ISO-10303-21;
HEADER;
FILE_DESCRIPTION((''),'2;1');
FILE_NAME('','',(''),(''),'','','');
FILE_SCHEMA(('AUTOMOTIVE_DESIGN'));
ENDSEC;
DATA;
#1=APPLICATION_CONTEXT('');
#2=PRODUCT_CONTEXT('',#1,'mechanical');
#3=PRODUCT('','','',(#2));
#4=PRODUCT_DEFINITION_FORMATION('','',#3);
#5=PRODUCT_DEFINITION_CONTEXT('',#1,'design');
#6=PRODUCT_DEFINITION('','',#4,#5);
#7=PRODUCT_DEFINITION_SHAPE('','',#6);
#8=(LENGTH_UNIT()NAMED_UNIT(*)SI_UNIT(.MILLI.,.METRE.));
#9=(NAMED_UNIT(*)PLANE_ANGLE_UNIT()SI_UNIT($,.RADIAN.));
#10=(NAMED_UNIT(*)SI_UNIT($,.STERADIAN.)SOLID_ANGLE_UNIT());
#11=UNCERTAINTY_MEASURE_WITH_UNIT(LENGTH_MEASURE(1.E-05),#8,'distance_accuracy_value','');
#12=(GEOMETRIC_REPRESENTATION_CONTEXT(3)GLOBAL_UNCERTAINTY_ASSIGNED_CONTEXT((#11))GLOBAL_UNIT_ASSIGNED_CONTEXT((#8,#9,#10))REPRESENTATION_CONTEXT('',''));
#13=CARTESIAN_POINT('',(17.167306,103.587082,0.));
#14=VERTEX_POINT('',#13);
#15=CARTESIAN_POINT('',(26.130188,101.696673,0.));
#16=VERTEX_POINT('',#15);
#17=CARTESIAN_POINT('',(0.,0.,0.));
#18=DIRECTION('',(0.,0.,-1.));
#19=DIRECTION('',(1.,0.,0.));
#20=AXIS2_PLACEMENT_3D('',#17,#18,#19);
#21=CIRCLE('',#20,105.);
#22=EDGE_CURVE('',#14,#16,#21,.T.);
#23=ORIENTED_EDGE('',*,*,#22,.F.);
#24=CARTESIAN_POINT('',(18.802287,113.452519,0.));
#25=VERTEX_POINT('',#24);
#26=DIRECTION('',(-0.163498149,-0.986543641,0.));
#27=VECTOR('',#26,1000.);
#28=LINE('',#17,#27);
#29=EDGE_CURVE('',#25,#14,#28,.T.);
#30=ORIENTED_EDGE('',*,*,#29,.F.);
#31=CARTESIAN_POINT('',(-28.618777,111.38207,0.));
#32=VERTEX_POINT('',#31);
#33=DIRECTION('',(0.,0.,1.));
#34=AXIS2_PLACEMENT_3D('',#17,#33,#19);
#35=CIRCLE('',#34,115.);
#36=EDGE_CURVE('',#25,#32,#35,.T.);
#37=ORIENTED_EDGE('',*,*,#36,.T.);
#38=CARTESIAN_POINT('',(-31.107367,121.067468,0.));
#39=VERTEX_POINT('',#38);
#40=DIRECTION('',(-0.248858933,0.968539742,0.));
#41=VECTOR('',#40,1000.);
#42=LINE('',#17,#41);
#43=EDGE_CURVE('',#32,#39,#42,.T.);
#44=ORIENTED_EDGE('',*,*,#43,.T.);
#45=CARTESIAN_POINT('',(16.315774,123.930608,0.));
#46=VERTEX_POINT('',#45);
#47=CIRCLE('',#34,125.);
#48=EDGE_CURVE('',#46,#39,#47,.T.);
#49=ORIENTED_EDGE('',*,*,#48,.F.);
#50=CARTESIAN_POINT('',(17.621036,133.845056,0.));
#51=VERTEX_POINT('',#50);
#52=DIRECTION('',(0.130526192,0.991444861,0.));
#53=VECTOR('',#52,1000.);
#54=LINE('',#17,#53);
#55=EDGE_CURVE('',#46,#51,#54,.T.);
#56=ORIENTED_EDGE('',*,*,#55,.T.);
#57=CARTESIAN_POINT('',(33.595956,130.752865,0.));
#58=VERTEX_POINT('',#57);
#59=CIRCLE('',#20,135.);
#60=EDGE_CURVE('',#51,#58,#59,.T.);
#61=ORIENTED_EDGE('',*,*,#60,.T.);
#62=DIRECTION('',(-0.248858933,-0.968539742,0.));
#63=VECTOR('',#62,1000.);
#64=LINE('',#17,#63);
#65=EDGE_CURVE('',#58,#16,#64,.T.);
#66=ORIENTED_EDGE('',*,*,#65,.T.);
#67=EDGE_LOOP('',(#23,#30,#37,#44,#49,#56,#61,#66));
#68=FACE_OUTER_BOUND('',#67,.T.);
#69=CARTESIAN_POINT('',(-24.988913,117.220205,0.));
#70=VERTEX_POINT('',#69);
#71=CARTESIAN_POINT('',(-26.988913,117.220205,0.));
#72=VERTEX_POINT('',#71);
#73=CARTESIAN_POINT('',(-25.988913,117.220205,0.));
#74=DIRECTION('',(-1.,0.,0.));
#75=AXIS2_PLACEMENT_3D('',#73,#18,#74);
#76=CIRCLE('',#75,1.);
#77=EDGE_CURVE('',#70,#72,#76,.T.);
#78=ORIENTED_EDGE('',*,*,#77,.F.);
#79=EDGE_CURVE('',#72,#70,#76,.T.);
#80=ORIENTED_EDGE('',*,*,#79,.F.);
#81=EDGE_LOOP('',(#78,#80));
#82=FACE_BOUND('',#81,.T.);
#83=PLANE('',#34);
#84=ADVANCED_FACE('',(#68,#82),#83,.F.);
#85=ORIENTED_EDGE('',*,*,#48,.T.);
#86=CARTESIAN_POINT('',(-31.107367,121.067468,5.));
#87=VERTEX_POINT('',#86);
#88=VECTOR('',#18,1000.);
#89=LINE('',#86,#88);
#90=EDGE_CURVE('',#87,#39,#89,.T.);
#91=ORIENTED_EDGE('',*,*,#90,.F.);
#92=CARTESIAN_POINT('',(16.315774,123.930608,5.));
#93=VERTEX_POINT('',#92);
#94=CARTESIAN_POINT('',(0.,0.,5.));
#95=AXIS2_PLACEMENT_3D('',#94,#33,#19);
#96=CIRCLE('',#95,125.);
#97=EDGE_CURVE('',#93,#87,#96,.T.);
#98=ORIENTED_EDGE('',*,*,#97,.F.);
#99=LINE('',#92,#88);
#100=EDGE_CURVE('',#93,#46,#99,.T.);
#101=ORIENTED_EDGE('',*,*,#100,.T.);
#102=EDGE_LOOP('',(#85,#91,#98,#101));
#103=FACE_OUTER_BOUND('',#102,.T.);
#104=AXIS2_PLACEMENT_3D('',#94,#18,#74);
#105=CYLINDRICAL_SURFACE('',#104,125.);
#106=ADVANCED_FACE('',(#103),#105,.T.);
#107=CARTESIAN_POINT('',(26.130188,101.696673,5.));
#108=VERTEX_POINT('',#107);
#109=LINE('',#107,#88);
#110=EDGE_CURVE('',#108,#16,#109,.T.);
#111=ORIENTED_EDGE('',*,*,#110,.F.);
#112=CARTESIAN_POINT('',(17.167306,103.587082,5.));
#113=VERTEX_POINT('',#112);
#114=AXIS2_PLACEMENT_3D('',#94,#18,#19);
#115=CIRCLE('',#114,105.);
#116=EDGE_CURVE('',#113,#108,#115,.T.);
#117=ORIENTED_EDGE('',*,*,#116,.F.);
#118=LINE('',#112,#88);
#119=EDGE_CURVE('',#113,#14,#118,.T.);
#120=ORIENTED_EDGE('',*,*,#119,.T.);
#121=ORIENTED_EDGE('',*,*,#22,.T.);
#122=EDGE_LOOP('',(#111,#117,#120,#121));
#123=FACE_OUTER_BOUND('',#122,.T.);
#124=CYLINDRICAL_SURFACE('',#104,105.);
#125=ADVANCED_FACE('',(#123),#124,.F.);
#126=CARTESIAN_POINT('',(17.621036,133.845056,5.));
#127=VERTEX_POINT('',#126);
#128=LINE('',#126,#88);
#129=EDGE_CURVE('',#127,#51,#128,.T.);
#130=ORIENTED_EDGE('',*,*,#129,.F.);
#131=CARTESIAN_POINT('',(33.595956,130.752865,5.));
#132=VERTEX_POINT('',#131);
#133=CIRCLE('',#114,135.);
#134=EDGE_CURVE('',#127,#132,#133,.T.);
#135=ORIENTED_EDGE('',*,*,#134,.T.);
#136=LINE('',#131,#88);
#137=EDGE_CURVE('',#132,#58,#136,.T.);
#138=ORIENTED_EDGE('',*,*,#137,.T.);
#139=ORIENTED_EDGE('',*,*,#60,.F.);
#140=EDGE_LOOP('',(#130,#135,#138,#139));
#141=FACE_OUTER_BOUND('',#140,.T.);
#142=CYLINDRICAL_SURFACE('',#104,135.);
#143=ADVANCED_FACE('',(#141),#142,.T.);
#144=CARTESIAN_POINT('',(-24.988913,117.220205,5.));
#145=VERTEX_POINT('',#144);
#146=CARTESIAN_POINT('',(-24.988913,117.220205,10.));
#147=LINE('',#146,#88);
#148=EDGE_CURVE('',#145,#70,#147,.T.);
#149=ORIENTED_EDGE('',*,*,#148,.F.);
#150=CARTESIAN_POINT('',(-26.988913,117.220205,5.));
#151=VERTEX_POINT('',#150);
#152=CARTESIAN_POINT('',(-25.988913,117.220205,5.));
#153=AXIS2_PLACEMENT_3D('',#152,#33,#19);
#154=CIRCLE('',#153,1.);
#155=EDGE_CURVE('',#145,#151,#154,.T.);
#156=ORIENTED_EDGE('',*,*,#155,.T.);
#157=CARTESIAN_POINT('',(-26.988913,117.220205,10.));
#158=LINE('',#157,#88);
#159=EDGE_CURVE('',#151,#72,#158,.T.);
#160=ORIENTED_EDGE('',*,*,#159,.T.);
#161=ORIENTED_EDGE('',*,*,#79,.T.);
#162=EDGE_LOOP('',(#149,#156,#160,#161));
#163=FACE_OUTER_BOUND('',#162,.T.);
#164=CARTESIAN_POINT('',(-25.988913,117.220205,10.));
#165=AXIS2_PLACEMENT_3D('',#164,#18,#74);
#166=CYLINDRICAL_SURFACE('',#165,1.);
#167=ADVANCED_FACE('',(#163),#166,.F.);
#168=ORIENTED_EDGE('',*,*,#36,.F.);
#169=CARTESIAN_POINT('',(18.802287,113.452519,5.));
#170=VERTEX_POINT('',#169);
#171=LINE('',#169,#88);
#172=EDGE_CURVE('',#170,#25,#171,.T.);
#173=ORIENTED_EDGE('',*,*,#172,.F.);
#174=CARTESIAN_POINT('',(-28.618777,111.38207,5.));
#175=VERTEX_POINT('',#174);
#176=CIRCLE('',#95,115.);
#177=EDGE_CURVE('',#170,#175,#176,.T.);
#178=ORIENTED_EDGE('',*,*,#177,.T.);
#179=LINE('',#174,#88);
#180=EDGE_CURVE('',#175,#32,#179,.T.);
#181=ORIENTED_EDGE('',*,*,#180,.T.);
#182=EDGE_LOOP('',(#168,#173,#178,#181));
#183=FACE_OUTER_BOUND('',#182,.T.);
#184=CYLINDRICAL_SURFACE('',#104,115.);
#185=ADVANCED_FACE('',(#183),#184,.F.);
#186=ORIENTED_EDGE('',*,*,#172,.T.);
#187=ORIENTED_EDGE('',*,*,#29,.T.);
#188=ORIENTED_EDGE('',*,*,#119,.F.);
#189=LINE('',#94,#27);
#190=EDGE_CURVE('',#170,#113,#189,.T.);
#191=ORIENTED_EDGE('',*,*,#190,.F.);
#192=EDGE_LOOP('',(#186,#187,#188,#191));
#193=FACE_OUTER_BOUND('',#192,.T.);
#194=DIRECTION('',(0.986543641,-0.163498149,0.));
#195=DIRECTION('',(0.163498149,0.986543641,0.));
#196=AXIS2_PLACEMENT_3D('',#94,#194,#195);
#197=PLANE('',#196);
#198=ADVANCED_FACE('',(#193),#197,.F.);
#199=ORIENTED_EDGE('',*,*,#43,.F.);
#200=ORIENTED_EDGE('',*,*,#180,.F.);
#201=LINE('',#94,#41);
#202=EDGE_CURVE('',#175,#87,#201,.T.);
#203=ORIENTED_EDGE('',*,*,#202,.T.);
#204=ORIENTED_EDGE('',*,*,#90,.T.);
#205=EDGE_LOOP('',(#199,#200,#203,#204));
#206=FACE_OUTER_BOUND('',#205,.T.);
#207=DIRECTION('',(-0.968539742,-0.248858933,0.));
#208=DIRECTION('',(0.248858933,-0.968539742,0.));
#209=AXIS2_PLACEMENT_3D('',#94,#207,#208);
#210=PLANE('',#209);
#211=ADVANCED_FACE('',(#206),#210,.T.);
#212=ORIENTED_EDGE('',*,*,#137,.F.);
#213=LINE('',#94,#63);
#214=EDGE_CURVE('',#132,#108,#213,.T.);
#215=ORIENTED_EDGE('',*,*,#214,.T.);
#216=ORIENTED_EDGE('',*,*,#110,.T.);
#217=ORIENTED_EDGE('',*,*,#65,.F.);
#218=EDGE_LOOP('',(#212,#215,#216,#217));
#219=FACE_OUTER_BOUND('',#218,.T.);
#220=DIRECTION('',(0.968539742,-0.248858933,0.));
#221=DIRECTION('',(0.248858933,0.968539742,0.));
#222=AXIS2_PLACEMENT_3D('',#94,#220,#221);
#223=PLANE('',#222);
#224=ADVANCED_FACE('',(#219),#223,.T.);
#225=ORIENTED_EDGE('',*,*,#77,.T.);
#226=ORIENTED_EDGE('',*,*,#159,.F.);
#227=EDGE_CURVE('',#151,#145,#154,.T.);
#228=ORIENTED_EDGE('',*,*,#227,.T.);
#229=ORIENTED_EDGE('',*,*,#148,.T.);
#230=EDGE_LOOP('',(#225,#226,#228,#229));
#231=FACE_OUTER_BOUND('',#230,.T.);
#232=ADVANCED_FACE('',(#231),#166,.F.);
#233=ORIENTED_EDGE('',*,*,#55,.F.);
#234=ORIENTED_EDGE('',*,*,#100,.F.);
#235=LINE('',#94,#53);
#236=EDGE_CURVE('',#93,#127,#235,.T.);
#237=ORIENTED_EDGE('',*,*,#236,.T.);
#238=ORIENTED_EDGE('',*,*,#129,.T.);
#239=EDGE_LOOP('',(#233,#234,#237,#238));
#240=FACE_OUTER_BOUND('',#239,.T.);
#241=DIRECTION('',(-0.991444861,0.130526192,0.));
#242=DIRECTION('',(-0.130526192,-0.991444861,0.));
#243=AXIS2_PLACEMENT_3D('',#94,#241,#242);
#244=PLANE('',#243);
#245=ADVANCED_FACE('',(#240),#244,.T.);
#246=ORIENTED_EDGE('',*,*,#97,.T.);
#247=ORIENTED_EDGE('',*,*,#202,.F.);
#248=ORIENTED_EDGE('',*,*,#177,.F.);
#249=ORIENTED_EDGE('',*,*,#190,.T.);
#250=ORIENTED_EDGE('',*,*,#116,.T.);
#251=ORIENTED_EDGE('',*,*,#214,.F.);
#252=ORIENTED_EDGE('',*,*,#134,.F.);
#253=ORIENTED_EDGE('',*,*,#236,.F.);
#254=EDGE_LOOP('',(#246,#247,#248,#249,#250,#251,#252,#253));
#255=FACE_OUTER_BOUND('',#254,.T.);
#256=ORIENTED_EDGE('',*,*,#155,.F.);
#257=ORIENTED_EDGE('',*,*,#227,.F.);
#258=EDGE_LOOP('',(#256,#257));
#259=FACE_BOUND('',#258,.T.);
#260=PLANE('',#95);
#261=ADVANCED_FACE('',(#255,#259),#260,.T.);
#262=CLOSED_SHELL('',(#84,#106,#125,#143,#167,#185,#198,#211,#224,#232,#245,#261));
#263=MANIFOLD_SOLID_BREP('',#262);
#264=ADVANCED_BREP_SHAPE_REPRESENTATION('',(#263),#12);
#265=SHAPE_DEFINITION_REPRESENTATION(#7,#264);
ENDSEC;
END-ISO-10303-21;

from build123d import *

# Parameters (mm, degrees)
BOSS_EXTRUDE3_DEPTH = 5
SKETCH3_R           = 1
CUT_EXTRUDE1_DEPTH  = 10


with BuildPart() as part:
    # Sketch1 → Boss-Extrude3 (new body)
    with BuildSketch(Plane.XY):
        with BuildLine():
            Line((26.130187968, 101.696672889), (28.618777298, 111.382070307))
            Line((28.618777298, 111.382070307), (31.107366629, 121.067467725))
            Line((31.107366629, 121.067467725), (33.595955959, 130.752865143))
            ThreePointArc((33.595955959, 130.752865143), (27.860620179, 132.093852405), (22.072250126, 133.183391511))
            ThreePointArc((22.072250126, 133.183391511), (19.849400241, 133.53277242), (17.62103595, 133.845056285))
            Line((17.62103595, 133.845056285), (16.315774028, 123.930607672))
            ThreePointArc((16.315774028, 123.930607672), (-7.533073444, 124.772804747), (-31.107366629, 121.067467725))
            Line((-31.107366629, 121.067467725), (-28.618777298, 111.382070307))
            ThreePointArc((-28.618777298, 111.382070307), (-5.016229547, 114.890545482), (18.802287144, 113.452518695))
            Line((18.802287144, 113.452518695), (17.167305653, 103.587082286))
            ThreePointArc((17.167305653, 103.587082286), (21.669371251, 102.739662982), (26.130187968, 101.696672889))
        make_face()
    extrude(amount=BOSS_EXTRUDE3_DEPTH)

    # Sketch3 → Cut-Extrude1 (cut)
    with BuildSketch(Plane(origin=(0, 0, 0), x_dir=(-1, 0, 0), z_dir=(0, 0, -1))):
        with Locations((25.988912996, 117.220204748)):
            Circle(SKETCH3_R)
    extrude(amount=-CUT_EXTRUDE1_DEPTH, mode=Mode.SUBTRACT)


solid = part.part
